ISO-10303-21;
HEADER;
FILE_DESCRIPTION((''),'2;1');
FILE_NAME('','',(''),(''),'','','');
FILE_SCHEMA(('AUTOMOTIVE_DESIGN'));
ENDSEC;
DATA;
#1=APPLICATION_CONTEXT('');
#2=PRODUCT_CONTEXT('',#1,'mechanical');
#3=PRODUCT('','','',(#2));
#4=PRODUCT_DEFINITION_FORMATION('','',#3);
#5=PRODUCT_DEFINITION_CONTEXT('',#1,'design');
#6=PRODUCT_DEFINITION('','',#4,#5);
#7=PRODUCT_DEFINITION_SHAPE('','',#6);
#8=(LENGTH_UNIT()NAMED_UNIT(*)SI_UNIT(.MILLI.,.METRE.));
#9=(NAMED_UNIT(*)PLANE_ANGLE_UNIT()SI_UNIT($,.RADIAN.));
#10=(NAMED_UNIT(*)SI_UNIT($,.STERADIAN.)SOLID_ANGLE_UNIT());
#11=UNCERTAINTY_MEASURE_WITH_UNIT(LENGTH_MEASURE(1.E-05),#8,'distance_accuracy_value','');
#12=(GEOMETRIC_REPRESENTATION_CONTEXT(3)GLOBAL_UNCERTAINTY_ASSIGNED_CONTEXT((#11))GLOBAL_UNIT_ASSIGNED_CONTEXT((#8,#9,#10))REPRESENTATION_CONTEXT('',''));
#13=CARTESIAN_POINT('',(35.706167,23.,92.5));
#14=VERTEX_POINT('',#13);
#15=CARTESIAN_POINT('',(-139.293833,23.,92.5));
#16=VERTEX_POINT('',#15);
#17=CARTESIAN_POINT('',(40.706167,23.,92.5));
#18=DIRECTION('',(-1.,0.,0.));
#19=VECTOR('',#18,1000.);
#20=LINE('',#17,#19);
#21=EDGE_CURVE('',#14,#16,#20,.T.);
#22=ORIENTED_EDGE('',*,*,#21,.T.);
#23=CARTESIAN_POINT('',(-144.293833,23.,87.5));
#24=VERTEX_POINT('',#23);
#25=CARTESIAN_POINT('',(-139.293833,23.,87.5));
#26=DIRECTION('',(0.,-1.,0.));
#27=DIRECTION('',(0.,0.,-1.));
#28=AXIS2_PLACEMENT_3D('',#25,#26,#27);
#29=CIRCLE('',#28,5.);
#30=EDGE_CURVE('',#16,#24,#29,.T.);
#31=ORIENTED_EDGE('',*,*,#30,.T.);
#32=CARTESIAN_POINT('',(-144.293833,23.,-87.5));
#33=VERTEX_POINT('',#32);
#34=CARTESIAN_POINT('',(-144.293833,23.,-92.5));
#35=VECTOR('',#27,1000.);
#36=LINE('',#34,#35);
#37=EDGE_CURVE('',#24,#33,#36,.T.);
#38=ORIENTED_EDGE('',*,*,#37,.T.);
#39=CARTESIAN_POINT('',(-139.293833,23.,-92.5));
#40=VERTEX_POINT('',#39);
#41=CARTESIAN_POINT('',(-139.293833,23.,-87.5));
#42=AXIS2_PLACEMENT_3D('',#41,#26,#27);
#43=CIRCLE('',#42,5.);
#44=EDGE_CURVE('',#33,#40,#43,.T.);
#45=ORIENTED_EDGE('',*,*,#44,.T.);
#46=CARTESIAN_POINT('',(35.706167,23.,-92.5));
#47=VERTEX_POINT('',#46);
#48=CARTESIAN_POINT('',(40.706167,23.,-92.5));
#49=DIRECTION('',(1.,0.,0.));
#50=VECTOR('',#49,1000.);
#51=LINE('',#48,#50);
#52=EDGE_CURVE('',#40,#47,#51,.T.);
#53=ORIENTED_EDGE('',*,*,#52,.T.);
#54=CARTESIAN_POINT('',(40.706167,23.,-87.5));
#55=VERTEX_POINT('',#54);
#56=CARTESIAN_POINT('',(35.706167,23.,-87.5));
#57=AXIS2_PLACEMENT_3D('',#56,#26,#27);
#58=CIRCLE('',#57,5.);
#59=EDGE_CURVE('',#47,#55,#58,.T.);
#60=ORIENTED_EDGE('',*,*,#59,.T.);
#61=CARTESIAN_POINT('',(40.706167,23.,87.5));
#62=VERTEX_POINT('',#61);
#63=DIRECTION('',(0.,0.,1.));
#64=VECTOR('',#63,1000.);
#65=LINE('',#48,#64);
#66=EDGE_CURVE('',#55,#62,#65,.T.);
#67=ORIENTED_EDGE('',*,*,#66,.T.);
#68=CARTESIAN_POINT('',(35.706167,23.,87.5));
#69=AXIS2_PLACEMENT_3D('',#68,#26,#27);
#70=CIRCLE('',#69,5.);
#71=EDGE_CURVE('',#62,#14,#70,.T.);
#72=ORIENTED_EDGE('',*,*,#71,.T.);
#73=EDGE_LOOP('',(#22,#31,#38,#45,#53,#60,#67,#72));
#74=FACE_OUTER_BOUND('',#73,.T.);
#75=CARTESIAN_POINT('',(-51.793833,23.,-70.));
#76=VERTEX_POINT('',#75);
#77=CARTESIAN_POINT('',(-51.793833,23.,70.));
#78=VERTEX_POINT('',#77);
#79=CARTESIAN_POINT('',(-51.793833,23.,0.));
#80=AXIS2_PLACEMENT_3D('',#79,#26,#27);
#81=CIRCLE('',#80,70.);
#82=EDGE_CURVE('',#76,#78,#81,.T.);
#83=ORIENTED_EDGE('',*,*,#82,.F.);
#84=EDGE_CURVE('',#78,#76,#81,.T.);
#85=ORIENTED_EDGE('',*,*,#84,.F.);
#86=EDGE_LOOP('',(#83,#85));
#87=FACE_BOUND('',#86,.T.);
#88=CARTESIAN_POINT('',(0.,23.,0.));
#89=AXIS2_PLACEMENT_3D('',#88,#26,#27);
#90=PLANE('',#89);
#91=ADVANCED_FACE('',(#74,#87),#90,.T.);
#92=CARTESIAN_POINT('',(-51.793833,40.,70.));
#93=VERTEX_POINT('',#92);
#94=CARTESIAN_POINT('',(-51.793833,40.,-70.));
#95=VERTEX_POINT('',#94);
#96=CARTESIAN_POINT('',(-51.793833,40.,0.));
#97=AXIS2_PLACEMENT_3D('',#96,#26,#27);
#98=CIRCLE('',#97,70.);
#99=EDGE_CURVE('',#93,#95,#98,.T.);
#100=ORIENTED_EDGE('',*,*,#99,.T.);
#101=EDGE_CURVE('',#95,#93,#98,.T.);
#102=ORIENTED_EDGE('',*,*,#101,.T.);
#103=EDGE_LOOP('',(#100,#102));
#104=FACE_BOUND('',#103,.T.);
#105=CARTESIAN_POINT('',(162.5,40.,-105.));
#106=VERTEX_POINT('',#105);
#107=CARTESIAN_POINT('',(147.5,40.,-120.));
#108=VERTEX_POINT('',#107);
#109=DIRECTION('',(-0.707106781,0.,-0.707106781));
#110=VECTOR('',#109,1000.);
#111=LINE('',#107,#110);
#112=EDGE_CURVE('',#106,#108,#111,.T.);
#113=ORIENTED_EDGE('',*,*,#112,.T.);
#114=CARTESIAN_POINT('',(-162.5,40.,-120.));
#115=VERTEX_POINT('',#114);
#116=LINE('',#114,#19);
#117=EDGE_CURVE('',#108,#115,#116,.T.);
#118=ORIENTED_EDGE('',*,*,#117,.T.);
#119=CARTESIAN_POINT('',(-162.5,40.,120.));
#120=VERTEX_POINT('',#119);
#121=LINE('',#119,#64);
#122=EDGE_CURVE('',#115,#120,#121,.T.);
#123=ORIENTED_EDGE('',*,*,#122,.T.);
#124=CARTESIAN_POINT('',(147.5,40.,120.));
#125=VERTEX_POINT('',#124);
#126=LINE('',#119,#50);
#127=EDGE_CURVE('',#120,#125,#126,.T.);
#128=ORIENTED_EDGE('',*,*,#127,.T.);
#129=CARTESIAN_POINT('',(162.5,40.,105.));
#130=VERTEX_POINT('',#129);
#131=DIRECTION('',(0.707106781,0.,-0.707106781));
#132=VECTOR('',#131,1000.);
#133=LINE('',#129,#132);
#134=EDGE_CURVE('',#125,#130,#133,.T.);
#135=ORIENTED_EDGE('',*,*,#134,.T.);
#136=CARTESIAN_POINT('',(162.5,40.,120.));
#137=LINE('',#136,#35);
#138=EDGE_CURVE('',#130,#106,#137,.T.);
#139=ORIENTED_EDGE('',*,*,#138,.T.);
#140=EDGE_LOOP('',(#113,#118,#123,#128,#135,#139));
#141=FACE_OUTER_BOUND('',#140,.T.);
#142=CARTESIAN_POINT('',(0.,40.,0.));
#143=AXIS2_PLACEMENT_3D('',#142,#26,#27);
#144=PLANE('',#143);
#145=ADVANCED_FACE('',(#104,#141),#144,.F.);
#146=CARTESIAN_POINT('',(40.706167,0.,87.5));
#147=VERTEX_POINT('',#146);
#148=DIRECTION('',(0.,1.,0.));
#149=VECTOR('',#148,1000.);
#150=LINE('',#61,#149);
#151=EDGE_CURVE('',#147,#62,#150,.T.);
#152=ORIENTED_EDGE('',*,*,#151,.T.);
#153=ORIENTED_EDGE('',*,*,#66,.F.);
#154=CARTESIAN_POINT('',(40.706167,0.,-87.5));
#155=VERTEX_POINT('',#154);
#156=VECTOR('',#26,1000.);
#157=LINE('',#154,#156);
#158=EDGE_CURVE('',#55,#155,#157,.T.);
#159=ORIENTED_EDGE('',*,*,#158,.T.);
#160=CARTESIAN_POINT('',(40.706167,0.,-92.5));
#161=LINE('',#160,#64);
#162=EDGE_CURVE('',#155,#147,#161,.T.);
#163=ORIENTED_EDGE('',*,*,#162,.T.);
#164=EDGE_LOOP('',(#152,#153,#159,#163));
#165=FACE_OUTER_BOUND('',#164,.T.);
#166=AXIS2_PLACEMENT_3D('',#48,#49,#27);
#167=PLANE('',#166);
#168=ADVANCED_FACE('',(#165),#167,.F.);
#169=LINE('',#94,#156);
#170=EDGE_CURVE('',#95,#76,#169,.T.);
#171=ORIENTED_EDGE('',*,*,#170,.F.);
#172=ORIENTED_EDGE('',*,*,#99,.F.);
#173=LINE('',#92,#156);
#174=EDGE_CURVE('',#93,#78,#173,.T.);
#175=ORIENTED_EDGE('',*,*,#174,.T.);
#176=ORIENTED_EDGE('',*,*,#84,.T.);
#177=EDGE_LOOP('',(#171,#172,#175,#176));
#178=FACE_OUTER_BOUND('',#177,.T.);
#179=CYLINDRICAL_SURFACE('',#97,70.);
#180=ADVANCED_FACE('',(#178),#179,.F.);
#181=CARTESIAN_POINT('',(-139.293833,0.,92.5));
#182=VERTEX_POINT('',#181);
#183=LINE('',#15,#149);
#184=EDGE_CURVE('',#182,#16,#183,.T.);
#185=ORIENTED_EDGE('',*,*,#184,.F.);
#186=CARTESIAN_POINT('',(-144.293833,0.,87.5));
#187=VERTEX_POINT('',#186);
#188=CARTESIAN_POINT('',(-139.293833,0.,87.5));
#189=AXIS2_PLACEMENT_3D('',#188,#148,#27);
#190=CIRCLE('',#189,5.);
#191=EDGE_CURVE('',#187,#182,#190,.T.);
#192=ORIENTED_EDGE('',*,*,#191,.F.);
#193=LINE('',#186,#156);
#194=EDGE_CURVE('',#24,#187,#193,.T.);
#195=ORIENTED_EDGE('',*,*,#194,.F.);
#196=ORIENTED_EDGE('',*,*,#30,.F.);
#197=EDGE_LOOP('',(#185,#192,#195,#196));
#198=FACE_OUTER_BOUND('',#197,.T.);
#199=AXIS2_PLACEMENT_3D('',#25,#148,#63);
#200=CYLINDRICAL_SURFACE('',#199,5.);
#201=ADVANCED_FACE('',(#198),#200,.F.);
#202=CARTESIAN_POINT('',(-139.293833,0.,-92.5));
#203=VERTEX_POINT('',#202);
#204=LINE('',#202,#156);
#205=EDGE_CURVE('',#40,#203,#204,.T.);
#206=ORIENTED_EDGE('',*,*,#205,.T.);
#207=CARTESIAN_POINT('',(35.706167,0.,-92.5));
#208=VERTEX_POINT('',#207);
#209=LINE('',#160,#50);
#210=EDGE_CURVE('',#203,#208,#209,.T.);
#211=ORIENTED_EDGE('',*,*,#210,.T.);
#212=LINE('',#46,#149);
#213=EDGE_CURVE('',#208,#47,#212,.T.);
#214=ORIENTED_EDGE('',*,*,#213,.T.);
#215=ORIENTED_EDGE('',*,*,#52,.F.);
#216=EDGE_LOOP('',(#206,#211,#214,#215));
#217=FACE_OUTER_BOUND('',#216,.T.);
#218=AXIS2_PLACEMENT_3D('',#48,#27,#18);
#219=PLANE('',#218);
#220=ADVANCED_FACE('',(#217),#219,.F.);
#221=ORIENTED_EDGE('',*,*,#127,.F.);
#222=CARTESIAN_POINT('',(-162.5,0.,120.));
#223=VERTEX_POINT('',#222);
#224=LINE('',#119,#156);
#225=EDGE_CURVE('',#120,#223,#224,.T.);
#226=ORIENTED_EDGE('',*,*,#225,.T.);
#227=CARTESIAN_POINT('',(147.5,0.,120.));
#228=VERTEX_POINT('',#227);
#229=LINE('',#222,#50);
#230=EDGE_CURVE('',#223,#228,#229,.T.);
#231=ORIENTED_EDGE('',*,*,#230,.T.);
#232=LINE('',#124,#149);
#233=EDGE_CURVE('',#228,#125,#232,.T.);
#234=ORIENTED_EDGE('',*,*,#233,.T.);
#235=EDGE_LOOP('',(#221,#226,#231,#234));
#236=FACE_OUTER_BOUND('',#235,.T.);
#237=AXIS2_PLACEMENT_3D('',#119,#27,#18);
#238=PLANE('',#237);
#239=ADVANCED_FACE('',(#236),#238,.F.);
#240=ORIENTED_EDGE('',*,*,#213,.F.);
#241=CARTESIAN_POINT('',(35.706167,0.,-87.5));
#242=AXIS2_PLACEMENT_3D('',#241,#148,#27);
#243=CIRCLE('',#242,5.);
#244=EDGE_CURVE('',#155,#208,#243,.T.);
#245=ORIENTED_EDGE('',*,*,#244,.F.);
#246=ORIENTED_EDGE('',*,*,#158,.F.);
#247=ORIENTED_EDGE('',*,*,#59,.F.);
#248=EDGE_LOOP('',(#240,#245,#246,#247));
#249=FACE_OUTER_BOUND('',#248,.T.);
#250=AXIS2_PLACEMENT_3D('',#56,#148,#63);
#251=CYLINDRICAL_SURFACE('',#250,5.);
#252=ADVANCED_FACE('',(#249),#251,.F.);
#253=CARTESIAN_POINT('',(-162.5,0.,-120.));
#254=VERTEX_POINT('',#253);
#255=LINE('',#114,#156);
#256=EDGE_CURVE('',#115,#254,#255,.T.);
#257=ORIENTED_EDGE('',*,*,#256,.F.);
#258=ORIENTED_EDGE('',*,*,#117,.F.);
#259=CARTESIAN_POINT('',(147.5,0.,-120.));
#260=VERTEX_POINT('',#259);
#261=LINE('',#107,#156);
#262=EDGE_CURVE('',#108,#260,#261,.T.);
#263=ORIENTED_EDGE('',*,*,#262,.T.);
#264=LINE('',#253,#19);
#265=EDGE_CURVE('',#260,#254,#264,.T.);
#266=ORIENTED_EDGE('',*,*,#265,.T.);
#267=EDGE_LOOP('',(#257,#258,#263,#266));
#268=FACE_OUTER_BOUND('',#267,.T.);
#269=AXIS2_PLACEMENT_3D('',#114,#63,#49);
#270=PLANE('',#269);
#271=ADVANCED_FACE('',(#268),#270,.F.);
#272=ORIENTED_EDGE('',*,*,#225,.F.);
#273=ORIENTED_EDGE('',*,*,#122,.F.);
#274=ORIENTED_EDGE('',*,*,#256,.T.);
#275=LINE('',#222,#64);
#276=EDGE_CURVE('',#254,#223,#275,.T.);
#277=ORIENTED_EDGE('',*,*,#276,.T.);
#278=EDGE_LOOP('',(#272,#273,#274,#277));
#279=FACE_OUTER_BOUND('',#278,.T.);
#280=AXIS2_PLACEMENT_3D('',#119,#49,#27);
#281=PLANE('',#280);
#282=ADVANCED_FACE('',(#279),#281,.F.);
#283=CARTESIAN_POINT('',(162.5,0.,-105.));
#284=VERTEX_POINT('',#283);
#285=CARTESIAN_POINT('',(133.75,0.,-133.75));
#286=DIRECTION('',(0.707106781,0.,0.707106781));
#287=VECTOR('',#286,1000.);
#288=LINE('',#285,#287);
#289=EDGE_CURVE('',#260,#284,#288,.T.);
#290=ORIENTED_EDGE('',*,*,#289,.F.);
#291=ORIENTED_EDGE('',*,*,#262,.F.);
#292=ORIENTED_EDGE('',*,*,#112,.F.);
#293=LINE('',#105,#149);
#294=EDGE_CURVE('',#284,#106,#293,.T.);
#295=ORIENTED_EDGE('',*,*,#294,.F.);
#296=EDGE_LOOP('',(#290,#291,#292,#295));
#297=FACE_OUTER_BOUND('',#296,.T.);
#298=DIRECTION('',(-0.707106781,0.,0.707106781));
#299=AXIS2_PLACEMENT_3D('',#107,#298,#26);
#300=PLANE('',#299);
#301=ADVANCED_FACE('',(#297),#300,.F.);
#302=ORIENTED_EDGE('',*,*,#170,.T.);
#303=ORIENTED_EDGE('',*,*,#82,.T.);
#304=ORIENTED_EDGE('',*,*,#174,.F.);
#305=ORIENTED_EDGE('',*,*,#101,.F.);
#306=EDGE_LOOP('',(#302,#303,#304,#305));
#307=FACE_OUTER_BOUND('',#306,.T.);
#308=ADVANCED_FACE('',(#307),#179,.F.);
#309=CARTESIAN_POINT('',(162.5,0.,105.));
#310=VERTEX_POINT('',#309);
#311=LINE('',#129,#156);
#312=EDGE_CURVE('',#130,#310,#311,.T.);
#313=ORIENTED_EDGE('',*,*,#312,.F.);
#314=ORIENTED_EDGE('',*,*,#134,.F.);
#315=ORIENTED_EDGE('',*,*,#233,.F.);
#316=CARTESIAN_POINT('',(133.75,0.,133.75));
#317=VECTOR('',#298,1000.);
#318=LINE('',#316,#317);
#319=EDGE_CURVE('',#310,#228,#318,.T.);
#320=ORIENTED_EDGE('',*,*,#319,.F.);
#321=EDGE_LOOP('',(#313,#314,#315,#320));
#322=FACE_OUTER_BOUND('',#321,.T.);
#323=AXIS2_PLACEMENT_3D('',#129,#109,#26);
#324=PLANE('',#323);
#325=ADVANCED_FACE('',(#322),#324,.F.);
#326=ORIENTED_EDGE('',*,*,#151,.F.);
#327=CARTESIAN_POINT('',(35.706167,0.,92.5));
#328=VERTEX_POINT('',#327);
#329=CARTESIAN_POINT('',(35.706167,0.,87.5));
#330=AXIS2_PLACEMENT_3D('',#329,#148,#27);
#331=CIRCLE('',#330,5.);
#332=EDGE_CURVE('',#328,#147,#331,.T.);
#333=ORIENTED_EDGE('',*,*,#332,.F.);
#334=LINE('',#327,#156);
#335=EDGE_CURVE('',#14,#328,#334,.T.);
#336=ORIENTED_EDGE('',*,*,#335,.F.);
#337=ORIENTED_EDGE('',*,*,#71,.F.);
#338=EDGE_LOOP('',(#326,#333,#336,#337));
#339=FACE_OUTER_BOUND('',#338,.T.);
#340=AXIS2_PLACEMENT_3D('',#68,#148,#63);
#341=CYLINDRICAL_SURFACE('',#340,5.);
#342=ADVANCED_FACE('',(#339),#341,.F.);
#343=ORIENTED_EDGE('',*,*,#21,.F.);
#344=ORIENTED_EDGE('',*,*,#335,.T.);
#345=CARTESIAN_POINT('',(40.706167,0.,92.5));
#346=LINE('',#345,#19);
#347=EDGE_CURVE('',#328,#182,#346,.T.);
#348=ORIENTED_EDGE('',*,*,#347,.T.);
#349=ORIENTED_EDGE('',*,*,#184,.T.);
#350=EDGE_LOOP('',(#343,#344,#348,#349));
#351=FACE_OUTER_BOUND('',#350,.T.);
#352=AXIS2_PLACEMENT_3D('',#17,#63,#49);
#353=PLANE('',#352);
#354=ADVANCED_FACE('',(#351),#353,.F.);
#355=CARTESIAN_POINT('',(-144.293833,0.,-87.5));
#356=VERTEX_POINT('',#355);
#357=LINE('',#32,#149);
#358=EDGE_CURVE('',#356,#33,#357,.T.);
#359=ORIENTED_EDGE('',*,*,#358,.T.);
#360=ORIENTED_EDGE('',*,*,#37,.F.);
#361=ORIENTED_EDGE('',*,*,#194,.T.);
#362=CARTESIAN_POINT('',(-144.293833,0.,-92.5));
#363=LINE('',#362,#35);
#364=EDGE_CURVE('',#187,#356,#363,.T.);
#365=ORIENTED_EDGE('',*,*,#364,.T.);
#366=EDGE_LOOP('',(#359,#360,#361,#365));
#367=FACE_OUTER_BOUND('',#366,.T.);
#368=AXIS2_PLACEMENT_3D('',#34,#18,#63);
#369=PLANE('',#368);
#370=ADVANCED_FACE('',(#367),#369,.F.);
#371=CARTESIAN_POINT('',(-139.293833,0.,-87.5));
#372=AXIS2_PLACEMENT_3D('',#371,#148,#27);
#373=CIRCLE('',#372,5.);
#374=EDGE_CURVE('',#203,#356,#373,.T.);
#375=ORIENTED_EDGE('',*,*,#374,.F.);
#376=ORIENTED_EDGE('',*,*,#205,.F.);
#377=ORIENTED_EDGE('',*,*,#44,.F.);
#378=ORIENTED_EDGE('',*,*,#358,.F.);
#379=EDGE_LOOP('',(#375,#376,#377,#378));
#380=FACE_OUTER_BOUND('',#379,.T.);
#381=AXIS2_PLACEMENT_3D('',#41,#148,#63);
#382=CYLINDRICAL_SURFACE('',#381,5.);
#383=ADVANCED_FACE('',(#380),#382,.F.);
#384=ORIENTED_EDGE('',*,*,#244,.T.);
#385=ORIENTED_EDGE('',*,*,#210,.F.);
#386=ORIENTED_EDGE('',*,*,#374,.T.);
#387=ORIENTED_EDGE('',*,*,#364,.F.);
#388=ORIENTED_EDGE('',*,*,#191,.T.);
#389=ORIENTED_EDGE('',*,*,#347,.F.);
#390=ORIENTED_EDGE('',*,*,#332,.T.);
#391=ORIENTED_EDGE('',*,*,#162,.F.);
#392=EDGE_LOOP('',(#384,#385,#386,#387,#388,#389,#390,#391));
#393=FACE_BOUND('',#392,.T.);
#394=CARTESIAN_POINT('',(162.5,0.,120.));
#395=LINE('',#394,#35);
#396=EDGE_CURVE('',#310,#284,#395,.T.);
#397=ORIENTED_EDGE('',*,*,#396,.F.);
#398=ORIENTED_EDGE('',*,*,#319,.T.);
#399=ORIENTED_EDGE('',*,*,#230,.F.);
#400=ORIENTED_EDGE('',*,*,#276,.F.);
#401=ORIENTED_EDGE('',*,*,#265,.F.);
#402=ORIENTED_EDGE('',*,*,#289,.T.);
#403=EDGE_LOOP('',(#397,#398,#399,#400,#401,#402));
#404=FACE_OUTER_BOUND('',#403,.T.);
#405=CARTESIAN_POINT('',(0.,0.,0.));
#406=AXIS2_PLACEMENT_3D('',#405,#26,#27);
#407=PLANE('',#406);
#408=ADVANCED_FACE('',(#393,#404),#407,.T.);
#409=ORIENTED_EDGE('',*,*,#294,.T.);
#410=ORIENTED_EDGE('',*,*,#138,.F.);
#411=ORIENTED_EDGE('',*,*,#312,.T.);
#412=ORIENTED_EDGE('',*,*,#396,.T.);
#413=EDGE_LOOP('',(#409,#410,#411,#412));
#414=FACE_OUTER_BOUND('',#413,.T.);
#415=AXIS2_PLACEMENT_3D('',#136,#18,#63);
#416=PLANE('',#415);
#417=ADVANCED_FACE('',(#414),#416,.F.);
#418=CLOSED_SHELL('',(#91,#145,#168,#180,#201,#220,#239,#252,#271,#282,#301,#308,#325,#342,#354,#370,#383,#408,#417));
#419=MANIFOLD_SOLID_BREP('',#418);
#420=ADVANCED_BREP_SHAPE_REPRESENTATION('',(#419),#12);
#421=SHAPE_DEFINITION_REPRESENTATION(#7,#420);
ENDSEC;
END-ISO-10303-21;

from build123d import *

# Parameters (mm, degrees)
SKETCH_1_W          = 325
SKETCH_1_H          = 240
EXTRUDE_1_DEPTH     = 40
SKETCH_2_W          = 185
SKETCH_2_H          = 185
CUT_EXTRUDE_1_DEPTH = 23
SKETCH_3_R          = 70
CUT_EXTRUDE_2_DEPTH = 204.310722787
FILLET_1_R          = 5
CHAMFER_1_SIZE      = 15


with BuildPart() as part:
    # 草图1 → 凸台-拉伸1 (new body)
    with BuildSketch(Plane(origin=(0, 0, 0), x_dir=(1, 0, 0), z_dir=(0, 1, 0))):
        Rectangle(SKETCH_1_W, SKETCH_1_H)
    extrude(amount=EXTRUDE_1_DEPTH)

    # 草图2 → 切除-拉伸1 (cut)
    with BuildSketch(Plane.XZ):
        with Locations((-51.793832524, 0)):
            Rectangle(SKETCH_2_W, SKETCH_2_H)
    extrude(amount=-CUT_EXTRUDE_1_DEPTH, mode=Mode.SUBTRACT)

    # 草图3 → 切除-拉伸2 (cut, through all)
    with BuildSketch(Plane.XZ.offset(-23)):
        with Locations(Location((-51.793832524, 0, 0), (0, 0, 270))):
            Circle(SKETCH_3_R)
    extrude(amount=-CUT_EXTRUDE_2_DEPTH, mode=Mode.SUBTRACT)

    # 圆角1
    fillet_1_edges = [part.edges().sort_by_distance(p)[0] for p in [
        (-144.293832524, 11.5, -92.5),
        (-144.293832524, 11.5, 92.5),
        (40.706167476, 11.5, 92.5),
        (40.706167476, 11.5, -92.5),
    ]]
    fillet(fillet_1_edges, radius=FILLET_1_R)

    # 倒角1
    chamfer_1_edges = [part.edges().sort_by_distance(p)[0] for p in [
        (162.5, 20, 120),
        (162.5, 20, -120),
    ]]
    chamfer(chamfer_1_edges, length=CHAMFER_1_SIZE)


solid = part.part
